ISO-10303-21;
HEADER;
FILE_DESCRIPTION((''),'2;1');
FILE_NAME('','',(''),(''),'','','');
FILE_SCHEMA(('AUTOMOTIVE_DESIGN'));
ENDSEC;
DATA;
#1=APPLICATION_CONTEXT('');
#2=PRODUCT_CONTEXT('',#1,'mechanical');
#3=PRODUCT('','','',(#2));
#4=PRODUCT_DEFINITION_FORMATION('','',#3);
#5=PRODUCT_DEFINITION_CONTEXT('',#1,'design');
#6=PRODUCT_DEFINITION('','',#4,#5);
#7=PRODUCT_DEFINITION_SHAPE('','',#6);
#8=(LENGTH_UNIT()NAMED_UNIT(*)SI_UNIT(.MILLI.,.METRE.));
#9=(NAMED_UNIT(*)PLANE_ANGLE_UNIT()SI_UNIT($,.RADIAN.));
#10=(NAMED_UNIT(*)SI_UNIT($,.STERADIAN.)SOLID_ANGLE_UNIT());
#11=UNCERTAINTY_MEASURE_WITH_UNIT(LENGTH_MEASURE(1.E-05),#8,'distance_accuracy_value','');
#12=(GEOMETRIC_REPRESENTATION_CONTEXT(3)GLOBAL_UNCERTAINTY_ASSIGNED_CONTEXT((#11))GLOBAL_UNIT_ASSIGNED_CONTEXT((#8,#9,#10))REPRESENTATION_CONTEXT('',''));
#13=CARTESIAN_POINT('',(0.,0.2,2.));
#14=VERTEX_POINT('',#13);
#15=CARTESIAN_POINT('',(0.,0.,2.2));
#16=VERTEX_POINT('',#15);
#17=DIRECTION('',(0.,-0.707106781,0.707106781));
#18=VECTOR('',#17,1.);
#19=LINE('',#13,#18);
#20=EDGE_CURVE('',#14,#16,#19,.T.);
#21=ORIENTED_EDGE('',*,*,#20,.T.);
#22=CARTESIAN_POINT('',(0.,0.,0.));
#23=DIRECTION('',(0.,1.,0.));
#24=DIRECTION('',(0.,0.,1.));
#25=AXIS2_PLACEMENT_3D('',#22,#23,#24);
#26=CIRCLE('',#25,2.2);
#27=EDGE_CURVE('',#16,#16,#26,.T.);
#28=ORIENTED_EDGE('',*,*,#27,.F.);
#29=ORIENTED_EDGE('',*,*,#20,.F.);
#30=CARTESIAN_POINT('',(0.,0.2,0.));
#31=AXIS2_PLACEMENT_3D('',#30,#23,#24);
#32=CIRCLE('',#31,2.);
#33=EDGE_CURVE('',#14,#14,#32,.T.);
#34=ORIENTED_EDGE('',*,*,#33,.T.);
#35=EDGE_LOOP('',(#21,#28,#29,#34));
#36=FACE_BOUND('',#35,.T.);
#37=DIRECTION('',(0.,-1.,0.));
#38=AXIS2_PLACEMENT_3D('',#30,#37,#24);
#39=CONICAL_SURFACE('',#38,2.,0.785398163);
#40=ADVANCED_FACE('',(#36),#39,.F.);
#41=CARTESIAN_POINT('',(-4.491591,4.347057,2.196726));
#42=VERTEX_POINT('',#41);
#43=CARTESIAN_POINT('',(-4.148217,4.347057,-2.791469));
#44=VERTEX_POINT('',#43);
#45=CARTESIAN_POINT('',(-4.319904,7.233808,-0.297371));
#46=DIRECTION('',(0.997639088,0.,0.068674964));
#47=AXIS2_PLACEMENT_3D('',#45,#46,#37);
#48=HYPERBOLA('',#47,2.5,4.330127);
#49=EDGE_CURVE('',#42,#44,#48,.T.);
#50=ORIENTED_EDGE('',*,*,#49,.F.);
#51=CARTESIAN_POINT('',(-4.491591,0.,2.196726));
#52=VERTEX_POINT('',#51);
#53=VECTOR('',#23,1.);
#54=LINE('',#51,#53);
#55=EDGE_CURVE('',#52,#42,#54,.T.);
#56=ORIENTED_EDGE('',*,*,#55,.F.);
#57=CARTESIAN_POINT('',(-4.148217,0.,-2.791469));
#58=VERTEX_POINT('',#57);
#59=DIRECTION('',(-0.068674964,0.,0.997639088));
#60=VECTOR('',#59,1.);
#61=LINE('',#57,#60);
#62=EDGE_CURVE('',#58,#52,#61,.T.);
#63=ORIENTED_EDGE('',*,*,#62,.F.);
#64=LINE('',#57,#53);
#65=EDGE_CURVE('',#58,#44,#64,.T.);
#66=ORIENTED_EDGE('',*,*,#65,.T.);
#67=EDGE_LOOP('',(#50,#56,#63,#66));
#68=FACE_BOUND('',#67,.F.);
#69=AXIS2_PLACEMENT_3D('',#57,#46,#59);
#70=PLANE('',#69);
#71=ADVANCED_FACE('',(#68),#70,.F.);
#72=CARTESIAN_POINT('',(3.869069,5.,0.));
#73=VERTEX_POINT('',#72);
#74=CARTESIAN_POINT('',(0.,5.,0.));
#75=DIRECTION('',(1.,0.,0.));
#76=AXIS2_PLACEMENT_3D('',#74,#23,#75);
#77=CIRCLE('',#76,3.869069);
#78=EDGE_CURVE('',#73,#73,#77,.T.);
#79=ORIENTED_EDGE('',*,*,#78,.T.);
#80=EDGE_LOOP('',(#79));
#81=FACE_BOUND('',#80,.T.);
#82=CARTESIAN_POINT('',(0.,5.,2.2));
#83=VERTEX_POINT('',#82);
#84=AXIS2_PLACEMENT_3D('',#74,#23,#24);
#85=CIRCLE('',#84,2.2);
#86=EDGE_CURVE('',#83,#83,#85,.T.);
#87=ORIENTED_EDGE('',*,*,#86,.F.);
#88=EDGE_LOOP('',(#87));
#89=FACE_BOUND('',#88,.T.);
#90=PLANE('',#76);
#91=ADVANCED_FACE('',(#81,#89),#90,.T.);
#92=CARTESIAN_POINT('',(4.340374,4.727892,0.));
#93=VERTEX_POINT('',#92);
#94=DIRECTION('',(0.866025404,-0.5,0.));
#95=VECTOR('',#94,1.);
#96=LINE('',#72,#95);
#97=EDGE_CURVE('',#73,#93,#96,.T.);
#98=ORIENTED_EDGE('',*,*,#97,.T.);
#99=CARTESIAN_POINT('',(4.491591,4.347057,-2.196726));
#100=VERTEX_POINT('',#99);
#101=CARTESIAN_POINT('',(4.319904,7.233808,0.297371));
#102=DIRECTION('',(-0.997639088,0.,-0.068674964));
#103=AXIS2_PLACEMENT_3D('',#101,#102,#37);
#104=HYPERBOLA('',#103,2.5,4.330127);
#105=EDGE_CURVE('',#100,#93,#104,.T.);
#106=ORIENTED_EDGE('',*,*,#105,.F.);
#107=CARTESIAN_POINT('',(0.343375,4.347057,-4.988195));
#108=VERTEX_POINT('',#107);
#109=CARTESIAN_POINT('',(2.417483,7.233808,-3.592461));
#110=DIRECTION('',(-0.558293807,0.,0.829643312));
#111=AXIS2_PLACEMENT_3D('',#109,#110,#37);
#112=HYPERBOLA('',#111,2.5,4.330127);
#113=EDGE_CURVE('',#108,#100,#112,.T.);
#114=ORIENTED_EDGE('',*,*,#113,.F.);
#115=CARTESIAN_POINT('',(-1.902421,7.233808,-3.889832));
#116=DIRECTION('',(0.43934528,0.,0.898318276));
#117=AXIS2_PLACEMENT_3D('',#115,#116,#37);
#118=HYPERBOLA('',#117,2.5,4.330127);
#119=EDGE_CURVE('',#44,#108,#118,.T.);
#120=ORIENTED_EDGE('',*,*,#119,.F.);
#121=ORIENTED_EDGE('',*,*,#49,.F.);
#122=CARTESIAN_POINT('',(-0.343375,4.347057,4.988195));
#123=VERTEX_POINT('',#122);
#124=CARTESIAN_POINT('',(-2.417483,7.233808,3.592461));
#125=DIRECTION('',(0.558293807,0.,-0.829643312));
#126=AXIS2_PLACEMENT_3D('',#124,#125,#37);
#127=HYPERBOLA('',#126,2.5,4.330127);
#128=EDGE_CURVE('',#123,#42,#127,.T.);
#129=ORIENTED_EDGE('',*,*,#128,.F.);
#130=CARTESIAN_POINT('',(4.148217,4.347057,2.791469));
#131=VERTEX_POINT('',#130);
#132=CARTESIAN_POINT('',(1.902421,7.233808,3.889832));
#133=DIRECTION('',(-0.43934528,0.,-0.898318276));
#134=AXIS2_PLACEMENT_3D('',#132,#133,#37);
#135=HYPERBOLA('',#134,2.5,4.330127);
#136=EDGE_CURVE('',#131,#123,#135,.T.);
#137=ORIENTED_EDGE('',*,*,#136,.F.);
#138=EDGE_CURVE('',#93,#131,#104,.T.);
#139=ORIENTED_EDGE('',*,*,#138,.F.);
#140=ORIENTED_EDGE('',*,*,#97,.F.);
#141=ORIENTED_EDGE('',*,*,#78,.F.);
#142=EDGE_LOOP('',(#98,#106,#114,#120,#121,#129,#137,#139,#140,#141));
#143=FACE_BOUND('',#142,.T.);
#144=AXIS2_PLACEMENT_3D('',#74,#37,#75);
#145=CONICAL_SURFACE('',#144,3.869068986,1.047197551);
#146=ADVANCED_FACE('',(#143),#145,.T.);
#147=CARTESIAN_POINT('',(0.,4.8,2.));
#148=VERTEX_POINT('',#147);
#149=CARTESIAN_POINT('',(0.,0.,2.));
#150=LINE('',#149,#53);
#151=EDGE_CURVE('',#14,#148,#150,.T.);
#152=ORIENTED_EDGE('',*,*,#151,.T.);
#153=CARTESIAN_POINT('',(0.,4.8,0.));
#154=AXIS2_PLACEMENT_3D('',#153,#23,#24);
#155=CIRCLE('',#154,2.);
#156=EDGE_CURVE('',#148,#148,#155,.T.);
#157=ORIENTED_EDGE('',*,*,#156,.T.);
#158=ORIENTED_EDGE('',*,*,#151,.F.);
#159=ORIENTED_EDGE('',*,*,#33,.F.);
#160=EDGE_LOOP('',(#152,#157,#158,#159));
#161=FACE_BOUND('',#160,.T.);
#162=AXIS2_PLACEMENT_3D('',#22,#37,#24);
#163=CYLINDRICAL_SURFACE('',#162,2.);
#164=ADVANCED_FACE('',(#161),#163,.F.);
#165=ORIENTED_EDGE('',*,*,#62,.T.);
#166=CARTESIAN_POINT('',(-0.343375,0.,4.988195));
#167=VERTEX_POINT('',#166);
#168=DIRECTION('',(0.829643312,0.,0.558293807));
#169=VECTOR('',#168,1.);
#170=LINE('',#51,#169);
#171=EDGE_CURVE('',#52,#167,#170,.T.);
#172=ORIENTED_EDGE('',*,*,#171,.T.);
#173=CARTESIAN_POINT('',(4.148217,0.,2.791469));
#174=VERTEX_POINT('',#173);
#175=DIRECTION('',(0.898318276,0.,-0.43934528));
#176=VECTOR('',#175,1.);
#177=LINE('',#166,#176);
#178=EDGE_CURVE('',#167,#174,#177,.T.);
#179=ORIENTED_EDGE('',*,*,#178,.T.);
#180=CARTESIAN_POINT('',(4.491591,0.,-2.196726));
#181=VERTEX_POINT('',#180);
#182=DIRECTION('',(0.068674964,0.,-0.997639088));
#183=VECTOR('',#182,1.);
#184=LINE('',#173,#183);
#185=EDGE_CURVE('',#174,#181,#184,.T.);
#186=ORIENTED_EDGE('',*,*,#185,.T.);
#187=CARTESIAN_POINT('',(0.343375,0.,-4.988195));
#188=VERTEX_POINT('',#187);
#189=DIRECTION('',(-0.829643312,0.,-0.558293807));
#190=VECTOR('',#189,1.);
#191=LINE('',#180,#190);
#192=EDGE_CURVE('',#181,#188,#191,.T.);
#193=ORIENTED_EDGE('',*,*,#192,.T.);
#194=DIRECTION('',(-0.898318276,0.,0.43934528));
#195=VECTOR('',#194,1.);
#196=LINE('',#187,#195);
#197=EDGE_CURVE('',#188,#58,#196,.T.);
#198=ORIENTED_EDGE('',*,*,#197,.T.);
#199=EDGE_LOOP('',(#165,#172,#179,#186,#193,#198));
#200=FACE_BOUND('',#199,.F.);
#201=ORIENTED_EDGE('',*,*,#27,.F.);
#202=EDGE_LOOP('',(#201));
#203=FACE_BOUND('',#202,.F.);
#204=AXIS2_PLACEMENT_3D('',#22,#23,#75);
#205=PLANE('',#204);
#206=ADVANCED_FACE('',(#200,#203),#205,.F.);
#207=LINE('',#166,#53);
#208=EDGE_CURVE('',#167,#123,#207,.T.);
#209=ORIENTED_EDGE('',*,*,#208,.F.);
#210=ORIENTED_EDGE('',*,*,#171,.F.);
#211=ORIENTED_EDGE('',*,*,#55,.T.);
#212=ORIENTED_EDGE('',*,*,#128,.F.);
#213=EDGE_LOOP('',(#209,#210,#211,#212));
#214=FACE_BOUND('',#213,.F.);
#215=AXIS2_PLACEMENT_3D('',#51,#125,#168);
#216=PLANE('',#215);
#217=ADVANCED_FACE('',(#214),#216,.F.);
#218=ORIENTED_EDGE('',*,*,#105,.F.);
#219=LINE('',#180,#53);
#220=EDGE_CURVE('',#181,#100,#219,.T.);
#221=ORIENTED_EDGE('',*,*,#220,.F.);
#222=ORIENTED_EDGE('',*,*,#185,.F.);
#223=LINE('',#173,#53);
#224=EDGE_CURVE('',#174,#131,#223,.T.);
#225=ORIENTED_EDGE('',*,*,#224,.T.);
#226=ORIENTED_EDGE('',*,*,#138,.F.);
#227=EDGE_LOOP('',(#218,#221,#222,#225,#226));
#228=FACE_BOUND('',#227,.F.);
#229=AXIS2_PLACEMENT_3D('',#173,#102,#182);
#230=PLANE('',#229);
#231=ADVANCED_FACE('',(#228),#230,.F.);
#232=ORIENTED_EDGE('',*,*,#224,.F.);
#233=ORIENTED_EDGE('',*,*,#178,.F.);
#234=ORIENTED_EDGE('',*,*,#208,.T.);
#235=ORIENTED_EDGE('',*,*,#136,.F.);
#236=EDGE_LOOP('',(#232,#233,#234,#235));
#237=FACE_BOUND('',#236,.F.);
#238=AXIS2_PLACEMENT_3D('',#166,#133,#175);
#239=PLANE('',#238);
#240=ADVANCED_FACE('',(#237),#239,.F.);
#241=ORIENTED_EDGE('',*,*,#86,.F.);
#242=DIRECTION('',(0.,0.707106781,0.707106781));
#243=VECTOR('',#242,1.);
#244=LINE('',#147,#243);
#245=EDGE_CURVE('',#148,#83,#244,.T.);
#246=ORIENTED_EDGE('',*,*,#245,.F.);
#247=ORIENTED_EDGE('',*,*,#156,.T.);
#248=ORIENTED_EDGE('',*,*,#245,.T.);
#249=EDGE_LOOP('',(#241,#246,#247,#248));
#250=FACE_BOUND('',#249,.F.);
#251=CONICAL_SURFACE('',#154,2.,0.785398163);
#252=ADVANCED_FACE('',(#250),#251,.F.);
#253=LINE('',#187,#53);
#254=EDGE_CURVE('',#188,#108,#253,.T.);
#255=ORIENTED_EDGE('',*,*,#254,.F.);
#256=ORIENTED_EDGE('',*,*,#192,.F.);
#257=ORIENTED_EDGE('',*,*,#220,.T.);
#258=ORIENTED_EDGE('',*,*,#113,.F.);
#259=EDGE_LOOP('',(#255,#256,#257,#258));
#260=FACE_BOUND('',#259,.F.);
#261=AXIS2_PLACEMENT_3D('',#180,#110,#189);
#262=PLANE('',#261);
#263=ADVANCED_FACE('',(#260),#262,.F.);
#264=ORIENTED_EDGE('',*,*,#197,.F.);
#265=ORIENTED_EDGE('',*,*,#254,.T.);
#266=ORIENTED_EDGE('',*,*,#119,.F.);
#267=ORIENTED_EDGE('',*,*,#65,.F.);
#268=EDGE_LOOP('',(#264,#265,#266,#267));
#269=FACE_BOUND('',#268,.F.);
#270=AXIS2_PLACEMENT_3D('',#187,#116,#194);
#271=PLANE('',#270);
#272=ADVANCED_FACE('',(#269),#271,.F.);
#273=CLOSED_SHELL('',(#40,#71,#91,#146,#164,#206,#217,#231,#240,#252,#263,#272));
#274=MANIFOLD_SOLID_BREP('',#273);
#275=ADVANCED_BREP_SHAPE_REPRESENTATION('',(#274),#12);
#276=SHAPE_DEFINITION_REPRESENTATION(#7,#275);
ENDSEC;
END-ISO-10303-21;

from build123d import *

# Parameters (mm, degrees)
SKETCH1_R           = 2
BOSS_EXTRUDE1_DEPTH = 5
SKETCH8_OUTSIDE_W   = 31.17
SKETCH8_OUTSIDE_H   = 32.162
SKETCH8_OUTSIDE_R   = 3.869068986
CUT_EXTRUDE1_DEPTH  = 5
CUT_EXTRUDE1_DRAFT  = -60
CHAMFER1_SIZE       = 0.2
CHAMFER2_SIZE       = 0.2


with BuildPart() as part:
    # Sketch1 → Boss-Extrude1 (new body)
    with BuildSketch(Plane(origin=(0, 0, 0), x_dir=(1, 0, 0), z_dir=(0, 1, 0))):
        Polygon((4.148216558, -2.791469037), (4.491591379, 2.196726401), (0.343374821, 4.988195438), (-4.148216558, 2.791469037), (-4.491591379, -2.196726401), (-0.343374821, -4.988195438), align=None)
        with Locations(Location((0, 0, 0), (0, 0, 270))):
            Circle(SKETCH1_R, mode=Mode.SUBTRACT)
    extrude(amount=BOSS_EXTRUDE1_DEPTH)


with BuildPart() as cut_extrude1_tool:
    # Sketch8 outside → Cut-Extrude1 (with draft: the straight prism first)
    with BuildSketch(Plane(origin=(0, 5, 0), x_dir=(1, 0, 0), z_dir=(0, 1, 0))):
        Rectangle(SKETCH8_OUTSIDE_W, SKETCH8_OUTSIDE_H)
        Circle(SKETCH8_OUTSIDE_R, mode=Mode.SUBTRACT)
    extrude(amount=-CUT_EXTRUDE1_DEPTH)
    # Cut-Extrude1: the draft: its side faces are tilted about the plane it starts from
    cut_extrude1_sides = [cut_extrude1_tool.faces().sort_by_distance(p)[0] for p in [
        (0, 2.5, 16.081),
        (15.585, 2.5, 0),
        (0, 2.5, -16.081),
        (-15.585, 2.5, 0),
        (-3.869068986, 2.5, 0),
    ]]
    draft(cut_extrude1_sides, Plane(origin=(0, 5, 0), x_dir=(1, 0, 0), z_dir=(0, 1, 0)), CUT_EXTRUDE1_DRAFT)


with BuildPart() as part_1:
    add(part.part)

    # Cut-Extrude1: cut by cut_extrude1_tool
    add(cut_extrude1_tool.part, mode=Mode.SUBTRACT)

    # Chamfer1
    chamfer1_edges = [part_1.edges().sort_by_distance(p)[0] for p in [
        (0, 5, -2),
    ]]
    chamfer(chamfer1_edges, length=CHAMFER1_SIZE)

    # Chamfer2
    chamfer2_edges = [part_1.edges().sort_by_distance(p)[0] for p in [
        (0, 0, -2),
    ]]
    chamfer(chamfer2_edges, length=CHAMFER2_SIZE)


solid = part_1.part
